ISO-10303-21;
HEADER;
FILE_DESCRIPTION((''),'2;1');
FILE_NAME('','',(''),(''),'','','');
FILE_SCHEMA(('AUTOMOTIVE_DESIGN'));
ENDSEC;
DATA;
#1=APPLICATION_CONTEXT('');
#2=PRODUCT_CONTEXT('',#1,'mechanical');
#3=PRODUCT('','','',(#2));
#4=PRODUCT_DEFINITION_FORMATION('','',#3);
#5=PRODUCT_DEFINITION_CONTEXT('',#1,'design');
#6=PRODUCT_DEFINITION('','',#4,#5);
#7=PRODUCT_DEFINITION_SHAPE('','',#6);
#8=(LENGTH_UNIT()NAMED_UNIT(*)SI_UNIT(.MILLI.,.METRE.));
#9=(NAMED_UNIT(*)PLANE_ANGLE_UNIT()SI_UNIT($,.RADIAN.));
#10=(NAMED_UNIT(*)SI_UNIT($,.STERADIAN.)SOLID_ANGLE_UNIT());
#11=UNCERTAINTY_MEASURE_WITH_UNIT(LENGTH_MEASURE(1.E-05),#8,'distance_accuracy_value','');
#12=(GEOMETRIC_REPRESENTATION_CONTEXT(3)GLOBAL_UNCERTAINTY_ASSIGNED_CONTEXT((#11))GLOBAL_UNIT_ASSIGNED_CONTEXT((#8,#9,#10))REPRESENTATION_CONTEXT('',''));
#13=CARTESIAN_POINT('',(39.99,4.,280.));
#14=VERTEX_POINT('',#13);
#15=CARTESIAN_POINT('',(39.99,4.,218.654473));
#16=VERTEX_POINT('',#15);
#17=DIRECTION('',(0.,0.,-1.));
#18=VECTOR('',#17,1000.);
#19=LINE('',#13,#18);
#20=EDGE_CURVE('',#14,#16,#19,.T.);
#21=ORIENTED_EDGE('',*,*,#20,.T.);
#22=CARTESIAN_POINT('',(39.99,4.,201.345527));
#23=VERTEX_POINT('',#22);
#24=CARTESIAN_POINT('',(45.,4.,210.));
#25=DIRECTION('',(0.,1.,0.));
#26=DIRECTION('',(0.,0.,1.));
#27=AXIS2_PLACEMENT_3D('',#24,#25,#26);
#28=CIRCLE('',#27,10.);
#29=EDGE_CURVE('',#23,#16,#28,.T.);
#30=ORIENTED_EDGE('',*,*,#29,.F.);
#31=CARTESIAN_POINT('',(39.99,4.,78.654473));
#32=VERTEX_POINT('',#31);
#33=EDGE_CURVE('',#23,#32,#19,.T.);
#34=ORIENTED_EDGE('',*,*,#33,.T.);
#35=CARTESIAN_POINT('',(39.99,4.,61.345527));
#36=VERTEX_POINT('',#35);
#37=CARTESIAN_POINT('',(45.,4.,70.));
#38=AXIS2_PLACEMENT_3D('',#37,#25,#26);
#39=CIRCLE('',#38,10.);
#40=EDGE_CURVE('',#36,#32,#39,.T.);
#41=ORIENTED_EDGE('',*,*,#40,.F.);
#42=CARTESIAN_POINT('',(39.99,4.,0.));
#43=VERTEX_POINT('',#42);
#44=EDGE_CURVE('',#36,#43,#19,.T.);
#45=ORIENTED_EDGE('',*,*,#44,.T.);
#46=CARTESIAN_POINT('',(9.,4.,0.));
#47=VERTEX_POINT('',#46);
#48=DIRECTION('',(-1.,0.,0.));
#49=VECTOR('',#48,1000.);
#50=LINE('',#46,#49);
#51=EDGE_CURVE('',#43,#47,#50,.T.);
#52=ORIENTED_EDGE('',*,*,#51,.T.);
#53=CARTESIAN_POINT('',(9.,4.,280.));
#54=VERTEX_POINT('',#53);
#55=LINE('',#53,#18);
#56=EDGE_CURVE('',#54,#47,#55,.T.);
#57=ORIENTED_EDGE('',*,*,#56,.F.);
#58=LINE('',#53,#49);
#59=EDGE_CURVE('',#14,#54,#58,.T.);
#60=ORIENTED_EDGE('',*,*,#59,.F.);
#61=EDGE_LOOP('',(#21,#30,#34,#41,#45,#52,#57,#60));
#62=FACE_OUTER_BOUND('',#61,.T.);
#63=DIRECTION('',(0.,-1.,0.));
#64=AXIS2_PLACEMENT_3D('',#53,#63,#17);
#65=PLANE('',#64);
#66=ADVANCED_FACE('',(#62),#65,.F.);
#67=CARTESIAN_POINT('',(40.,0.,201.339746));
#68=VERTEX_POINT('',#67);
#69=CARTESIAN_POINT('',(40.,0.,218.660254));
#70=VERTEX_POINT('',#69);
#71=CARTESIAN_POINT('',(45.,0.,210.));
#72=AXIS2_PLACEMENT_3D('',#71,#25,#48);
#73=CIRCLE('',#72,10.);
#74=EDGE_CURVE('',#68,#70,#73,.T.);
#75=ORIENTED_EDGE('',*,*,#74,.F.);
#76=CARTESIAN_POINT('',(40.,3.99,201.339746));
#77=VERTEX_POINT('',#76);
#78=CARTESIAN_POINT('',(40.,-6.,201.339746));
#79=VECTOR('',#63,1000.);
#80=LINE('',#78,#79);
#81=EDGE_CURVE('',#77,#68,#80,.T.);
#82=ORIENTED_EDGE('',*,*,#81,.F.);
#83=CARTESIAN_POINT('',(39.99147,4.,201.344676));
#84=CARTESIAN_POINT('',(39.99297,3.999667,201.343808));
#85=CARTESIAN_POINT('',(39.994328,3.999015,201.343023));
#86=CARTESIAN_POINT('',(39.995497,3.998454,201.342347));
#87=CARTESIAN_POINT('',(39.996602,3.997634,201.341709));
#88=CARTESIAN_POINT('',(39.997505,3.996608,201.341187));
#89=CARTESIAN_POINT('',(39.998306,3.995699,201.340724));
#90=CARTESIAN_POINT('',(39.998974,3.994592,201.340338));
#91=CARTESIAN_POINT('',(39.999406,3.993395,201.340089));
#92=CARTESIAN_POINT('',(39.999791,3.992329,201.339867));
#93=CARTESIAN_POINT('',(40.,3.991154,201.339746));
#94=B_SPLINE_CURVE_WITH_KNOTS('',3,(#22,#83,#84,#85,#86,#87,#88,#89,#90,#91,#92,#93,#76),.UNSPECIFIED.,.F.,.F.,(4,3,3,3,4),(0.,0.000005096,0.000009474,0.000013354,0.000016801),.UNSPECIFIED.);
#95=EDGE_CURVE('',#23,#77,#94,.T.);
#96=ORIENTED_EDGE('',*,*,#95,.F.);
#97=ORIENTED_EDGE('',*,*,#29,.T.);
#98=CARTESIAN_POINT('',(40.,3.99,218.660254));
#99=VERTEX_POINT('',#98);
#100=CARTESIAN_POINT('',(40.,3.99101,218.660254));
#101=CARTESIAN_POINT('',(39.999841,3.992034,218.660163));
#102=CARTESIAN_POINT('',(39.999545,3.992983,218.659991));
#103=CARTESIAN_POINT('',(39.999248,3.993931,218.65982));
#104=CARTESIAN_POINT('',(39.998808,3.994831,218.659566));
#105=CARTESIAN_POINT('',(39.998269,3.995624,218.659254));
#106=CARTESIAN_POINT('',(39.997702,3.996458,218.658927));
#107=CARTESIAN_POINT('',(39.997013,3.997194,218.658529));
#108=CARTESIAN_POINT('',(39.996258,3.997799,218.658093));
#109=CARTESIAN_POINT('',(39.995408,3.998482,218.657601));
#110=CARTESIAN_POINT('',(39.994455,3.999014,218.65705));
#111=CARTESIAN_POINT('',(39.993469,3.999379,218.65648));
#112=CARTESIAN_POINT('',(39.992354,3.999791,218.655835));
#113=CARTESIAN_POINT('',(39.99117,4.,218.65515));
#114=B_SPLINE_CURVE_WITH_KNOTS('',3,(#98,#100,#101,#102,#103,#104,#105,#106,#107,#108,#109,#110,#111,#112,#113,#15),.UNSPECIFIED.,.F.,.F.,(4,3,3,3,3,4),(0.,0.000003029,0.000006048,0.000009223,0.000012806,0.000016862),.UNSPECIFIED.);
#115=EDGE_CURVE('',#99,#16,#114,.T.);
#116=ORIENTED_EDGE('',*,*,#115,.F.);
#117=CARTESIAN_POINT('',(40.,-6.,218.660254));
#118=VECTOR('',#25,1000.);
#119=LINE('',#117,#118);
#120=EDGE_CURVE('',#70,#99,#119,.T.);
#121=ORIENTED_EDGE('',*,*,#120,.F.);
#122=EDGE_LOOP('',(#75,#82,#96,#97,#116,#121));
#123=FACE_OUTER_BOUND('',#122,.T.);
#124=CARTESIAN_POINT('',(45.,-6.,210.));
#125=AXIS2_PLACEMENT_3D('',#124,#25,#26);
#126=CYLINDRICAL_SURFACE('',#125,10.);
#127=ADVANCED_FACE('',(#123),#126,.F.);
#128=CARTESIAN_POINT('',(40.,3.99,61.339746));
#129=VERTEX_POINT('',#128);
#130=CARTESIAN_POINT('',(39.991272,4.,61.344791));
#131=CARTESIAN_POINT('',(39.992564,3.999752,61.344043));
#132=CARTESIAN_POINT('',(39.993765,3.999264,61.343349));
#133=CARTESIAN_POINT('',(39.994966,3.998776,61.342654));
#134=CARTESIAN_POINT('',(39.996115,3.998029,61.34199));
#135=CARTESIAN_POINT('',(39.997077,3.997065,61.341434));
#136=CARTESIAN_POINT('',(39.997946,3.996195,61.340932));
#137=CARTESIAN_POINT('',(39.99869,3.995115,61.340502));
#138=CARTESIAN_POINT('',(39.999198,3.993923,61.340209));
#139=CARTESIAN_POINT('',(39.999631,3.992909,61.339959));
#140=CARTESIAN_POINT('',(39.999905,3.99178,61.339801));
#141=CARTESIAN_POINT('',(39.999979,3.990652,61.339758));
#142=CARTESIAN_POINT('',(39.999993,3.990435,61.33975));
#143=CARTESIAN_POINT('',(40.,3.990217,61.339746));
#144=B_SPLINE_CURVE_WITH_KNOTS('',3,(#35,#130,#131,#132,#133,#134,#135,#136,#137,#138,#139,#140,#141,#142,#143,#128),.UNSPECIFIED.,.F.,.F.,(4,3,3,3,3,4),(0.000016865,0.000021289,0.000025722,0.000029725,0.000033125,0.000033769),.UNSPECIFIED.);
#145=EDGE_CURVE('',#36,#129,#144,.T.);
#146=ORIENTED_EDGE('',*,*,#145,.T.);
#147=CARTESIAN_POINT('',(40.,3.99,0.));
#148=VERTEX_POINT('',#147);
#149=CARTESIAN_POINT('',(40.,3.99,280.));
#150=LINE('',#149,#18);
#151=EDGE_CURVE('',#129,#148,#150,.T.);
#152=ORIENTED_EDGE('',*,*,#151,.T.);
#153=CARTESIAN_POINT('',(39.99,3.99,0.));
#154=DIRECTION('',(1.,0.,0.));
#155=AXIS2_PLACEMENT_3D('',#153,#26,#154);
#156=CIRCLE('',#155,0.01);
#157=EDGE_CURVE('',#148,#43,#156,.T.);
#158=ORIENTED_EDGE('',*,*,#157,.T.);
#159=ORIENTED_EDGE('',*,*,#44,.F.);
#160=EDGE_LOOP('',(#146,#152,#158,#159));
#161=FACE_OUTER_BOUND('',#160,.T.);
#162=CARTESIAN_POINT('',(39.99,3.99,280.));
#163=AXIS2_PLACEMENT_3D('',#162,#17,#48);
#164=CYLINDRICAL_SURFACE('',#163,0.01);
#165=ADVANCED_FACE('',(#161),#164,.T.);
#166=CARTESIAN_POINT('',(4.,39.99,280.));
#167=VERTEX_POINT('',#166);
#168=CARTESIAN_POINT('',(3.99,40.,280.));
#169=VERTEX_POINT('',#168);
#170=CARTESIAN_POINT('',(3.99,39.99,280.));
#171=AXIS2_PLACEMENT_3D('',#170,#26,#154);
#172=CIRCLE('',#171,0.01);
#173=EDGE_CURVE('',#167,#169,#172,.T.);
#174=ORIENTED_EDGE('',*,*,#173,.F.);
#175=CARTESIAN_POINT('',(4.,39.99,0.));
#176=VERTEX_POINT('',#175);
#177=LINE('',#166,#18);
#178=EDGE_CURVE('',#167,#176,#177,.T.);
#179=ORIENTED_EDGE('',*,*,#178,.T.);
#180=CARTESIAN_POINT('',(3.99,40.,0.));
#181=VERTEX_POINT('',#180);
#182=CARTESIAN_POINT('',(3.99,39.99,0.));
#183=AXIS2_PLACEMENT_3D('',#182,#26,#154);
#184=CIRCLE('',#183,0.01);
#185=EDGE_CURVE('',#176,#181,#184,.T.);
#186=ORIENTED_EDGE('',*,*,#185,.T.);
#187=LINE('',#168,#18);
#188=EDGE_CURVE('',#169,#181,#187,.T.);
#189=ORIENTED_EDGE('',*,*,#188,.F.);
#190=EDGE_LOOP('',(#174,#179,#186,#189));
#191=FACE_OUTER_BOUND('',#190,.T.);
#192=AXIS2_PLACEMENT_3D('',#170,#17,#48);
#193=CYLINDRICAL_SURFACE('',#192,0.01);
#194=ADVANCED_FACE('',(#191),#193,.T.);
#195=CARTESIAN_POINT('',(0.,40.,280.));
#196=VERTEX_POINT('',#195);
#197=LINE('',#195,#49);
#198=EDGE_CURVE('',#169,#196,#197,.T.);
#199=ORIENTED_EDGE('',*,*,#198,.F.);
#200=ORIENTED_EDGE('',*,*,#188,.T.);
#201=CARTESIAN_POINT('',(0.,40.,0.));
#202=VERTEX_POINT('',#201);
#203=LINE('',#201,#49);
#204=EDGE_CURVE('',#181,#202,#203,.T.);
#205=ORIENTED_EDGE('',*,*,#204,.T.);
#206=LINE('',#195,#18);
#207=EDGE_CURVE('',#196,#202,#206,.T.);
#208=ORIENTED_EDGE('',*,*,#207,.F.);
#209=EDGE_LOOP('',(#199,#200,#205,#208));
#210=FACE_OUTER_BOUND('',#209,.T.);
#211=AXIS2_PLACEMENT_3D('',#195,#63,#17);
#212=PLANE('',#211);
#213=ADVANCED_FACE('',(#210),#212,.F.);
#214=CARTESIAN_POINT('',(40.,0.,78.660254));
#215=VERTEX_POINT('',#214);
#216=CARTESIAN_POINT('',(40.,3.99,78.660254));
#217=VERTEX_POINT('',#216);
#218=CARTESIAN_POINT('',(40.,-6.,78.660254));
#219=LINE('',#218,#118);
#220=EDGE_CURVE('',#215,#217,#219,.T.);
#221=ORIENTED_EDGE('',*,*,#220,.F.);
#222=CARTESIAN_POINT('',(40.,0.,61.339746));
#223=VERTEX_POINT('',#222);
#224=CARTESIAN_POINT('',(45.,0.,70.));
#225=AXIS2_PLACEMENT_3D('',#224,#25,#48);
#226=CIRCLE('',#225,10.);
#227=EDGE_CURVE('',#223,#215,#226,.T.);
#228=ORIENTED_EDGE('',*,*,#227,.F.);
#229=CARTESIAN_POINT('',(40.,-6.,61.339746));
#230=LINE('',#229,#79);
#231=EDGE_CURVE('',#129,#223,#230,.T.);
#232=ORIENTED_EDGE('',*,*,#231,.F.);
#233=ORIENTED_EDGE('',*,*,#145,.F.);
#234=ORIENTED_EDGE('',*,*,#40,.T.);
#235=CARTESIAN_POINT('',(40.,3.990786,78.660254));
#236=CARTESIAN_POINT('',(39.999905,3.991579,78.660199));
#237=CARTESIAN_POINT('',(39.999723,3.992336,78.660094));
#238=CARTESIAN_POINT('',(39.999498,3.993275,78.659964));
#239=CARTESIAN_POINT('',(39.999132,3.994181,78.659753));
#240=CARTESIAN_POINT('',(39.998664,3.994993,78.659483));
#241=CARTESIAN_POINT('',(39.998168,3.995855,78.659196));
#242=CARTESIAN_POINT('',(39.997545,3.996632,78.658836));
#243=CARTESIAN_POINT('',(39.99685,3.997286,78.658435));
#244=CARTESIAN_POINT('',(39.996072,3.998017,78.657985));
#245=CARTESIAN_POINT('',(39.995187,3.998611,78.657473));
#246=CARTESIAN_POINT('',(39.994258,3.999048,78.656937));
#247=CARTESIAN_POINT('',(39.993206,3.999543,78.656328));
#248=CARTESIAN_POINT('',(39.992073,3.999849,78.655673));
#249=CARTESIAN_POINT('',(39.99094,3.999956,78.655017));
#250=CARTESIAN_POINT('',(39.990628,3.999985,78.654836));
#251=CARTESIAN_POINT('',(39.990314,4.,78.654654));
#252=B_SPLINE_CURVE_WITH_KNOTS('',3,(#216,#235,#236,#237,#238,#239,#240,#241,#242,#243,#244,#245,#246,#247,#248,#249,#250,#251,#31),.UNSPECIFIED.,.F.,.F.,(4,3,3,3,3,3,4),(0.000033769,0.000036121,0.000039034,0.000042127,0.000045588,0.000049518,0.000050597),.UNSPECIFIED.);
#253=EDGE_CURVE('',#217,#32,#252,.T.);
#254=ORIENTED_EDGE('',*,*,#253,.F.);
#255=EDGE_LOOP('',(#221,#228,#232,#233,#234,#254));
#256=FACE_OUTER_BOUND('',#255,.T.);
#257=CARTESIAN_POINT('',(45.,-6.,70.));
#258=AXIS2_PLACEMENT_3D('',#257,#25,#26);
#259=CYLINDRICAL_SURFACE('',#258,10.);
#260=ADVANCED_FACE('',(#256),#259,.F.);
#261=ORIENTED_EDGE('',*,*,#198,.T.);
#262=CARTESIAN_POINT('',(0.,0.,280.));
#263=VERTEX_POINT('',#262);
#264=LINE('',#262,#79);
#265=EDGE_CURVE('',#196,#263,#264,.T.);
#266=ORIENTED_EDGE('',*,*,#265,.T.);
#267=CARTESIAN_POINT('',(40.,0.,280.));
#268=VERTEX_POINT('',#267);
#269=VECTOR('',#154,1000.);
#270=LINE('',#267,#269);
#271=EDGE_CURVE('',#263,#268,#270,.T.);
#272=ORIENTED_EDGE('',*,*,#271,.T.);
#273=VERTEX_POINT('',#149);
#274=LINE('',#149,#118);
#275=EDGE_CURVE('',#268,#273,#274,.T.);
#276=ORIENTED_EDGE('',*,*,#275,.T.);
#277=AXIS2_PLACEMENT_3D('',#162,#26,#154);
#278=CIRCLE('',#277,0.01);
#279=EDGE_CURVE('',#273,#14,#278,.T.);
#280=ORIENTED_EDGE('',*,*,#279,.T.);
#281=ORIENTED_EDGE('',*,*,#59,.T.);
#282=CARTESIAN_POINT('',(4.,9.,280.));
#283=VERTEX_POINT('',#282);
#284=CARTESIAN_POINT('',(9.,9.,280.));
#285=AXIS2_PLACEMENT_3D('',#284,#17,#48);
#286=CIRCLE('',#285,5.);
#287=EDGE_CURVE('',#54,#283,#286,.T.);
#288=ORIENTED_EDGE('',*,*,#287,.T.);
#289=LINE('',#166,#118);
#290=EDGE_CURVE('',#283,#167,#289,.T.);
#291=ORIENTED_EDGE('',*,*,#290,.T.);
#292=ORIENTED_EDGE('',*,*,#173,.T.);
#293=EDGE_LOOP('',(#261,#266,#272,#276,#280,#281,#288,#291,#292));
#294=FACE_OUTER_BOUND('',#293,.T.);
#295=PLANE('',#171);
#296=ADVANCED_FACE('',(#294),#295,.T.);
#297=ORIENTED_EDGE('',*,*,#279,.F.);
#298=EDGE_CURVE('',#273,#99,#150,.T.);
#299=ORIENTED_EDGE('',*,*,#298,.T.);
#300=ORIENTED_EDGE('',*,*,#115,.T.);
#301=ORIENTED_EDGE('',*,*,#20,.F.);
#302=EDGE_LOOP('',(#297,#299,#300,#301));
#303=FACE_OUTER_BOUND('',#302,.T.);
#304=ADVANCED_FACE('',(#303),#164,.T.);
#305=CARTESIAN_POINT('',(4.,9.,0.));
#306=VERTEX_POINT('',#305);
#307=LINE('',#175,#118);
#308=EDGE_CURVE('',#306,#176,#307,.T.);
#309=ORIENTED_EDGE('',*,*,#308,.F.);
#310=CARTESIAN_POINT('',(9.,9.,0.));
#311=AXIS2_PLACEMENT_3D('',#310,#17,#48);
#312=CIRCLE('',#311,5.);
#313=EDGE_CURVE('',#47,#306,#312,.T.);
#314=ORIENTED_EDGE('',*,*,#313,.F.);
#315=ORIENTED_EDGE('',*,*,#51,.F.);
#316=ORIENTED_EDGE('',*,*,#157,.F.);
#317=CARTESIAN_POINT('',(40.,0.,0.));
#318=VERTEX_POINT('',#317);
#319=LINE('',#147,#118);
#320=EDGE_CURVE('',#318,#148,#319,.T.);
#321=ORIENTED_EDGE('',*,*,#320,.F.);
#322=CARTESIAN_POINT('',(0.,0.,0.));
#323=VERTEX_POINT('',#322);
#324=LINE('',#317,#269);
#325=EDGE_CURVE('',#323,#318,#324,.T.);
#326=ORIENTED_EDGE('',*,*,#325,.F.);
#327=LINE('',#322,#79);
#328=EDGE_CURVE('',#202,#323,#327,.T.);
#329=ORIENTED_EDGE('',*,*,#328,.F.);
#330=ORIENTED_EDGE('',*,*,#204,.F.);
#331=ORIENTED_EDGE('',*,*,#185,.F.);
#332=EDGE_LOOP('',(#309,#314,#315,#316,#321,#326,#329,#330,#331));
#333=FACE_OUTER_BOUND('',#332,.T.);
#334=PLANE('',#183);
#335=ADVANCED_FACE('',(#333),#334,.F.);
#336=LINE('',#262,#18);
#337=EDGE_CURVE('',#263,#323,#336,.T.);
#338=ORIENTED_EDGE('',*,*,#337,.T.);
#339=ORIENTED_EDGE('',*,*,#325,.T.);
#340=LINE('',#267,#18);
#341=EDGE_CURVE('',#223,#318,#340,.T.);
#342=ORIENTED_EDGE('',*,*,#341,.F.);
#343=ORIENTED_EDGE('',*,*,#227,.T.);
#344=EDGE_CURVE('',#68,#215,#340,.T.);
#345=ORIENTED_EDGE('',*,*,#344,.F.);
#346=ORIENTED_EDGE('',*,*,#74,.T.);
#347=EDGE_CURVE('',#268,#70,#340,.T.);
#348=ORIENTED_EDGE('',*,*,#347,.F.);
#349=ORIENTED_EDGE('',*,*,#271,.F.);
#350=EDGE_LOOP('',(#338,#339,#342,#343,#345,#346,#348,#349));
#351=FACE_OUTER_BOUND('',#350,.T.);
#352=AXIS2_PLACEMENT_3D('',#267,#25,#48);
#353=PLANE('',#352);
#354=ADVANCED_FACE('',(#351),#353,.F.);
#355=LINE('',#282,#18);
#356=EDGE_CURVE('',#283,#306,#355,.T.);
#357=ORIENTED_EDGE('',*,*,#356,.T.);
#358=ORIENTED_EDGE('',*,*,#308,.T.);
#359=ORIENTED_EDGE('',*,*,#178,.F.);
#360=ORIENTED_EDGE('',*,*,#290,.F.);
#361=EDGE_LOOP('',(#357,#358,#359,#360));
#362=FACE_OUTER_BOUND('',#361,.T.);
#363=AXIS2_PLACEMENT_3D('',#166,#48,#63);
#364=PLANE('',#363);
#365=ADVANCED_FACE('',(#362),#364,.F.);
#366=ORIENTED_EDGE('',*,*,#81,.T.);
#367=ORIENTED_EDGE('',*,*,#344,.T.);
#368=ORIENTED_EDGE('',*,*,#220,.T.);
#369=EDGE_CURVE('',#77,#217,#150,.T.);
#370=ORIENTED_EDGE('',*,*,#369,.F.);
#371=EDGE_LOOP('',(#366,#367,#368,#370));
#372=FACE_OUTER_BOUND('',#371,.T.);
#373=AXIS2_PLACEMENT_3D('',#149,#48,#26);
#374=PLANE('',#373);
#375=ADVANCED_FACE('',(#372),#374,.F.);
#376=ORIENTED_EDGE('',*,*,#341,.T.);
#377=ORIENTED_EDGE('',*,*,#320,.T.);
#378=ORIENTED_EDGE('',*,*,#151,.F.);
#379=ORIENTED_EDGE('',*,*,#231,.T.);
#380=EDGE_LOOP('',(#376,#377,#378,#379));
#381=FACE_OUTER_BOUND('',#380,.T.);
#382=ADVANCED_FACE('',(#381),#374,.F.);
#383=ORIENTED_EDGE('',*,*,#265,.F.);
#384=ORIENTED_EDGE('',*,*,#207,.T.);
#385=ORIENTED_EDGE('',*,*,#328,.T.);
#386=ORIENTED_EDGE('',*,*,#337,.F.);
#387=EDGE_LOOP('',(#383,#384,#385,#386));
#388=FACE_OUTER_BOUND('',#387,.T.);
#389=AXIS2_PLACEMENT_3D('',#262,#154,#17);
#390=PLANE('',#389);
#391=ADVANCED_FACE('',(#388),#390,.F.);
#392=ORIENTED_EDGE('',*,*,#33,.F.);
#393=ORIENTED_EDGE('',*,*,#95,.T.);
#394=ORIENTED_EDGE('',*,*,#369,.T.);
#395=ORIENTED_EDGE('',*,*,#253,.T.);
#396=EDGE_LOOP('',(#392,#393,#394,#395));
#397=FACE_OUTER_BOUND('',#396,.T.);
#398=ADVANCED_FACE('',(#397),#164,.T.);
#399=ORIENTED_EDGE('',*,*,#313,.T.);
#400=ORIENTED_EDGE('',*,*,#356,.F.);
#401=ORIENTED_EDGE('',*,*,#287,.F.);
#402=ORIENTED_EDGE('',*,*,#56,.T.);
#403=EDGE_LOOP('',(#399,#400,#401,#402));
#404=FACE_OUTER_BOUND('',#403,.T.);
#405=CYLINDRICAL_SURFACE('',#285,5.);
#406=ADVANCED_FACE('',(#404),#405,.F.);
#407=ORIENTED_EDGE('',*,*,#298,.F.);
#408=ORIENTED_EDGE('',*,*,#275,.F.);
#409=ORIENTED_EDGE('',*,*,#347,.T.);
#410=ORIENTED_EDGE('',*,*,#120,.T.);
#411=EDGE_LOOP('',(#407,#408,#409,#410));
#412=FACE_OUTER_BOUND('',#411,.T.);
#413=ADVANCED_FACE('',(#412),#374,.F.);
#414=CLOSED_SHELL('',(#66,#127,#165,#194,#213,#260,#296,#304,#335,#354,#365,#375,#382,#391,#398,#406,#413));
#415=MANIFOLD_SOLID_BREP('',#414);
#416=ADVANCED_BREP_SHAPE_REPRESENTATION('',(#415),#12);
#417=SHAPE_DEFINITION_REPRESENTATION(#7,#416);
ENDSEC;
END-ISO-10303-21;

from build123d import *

# Parameters (mm, degrees)
EXTRUDE_1_DEPTH     = 280
SKETCH_2_R          = 10
CUT_EXTRUDE_1_DEPTH = 10


with BuildPart() as part:
    # 草图1 → 拉伸1 (new body)
    with BuildSketch(Plane.XY):
        with BuildLine():
            Line((0, 0), (0, 40))
            Line((0, 40), (3.99, 40))
            ThreePointArc((3.99, 40), (3.997071068, 39.997071068), (4, 39.99))
            Line((4, 39.99), (4, 9))
            ThreePointArc((4, 9), (5.464466094, 5.464466094), (9, 4))
            Line((9, 4), (39.99, 4))
            ThreePointArc((39.99, 4), (39.997071068, 3.997071068), (40, 3.99))
            Line((40, 3.99), (40, 0))
            Line((40, 0), (0, 0))
        make_face()
    extrude(amount=EXTRUDE_1_DEPTH)

    # 草图2 → 切除-拉伸1 (cut)
    with BuildSketch(Plane(origin=(0, 4, 0), x_dir=(1, 0, 0), z_dir=(0, 1, 0))):
        with Locations((45, -210)):
            Circle(SKETCH_2_R)
        with Locations((45, -70)):
            Circle(SKETCH_2_R)
    extrude(amount=-CUT_EXTRUDE_1_DEPTH, mode=Mode.SUBTRACT)


solid = part.part
